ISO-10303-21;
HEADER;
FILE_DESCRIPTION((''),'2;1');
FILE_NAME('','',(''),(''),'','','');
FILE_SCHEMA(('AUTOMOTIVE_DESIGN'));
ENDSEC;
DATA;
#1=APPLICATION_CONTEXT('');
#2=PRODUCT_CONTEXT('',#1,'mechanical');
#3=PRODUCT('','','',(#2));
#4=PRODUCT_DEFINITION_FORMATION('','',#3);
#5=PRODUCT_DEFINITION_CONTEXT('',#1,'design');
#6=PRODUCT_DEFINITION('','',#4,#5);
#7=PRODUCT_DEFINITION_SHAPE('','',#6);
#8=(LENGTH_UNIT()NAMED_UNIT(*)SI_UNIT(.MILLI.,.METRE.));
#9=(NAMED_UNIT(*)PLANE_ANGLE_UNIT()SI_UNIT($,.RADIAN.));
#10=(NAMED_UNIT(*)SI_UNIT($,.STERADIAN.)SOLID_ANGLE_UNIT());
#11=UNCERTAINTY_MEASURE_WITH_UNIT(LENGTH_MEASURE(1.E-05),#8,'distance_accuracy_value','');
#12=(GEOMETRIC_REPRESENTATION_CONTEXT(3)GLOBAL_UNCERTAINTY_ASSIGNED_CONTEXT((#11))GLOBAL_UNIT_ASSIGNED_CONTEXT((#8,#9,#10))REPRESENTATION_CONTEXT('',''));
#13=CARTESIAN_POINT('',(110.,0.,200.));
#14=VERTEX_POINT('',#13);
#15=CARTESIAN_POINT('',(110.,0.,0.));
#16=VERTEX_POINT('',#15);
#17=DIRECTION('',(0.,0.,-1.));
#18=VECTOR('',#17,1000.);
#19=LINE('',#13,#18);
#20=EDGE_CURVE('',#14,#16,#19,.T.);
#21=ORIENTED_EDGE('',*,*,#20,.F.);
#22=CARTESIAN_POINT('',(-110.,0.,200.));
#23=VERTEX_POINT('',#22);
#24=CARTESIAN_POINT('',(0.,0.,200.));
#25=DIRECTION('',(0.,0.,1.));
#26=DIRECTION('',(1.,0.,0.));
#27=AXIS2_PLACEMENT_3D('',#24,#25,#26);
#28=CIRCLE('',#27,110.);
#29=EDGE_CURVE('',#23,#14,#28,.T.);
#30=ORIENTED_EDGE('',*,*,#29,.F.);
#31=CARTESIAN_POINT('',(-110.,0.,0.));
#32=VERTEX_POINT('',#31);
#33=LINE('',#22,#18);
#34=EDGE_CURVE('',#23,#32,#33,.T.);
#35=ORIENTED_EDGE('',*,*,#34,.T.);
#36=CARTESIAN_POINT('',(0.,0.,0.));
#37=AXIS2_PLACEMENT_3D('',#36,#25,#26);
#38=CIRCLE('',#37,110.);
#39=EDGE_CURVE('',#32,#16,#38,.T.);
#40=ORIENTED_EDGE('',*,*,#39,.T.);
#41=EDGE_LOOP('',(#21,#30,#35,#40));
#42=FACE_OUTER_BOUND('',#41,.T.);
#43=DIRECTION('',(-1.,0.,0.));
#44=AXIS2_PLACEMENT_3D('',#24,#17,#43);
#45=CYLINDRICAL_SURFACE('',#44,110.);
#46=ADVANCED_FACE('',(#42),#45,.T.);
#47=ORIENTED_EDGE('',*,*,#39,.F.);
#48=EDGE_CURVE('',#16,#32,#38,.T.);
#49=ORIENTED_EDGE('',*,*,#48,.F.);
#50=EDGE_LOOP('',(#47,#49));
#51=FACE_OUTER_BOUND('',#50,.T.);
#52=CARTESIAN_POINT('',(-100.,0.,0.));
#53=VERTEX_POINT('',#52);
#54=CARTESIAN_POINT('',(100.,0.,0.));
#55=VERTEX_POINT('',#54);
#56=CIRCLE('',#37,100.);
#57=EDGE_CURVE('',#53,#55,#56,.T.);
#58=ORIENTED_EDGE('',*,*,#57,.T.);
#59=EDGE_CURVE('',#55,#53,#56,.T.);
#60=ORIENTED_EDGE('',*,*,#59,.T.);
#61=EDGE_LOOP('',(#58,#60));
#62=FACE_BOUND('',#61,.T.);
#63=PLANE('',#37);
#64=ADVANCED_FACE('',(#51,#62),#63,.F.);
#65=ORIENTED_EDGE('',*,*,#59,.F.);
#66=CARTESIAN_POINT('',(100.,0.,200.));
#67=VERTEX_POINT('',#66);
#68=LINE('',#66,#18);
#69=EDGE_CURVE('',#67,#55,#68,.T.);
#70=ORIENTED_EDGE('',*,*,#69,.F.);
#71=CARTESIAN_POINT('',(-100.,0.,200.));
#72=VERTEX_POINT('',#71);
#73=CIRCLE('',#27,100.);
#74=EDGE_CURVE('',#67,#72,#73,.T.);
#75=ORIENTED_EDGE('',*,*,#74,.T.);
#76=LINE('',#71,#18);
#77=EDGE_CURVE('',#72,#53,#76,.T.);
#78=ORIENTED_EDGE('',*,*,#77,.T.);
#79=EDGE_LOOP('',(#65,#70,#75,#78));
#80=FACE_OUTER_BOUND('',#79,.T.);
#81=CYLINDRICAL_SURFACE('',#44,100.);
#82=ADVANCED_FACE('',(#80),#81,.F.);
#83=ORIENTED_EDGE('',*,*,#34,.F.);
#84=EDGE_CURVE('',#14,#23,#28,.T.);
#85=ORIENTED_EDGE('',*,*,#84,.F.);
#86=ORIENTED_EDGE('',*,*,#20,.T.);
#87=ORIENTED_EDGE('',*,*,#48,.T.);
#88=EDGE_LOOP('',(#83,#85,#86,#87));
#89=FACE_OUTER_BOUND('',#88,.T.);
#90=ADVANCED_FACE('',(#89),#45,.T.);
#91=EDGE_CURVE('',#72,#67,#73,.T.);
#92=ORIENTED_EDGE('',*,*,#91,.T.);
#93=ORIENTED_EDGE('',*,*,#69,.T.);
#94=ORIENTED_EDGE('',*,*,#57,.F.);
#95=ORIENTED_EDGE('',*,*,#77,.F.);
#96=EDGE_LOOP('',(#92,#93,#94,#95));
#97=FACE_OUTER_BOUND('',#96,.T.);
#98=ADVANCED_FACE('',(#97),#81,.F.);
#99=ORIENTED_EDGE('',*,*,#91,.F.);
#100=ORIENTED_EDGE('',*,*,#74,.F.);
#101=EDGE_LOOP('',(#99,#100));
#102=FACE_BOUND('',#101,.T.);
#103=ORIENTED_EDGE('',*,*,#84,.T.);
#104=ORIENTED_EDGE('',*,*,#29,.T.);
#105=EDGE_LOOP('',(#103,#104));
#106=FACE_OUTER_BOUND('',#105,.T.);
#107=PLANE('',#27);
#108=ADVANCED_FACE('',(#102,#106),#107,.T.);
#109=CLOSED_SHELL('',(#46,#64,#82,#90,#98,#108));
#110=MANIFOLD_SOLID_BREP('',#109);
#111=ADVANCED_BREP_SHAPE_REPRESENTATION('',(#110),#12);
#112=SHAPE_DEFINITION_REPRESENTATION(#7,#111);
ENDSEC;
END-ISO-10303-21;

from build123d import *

# Parameters (mm, degrees)
SKETCH_1_R      = 110
SKETCH_1_R_2    = 100
EXTRUDE_1_DEPTH = 200


with BuildPart() as part:
    # 草图1 → 拉伸-薄壁1 (new body)
    with BuildSketch(Plane.XY):
        Circle(SKETCH_1_R)
        Circle(SKETCH_1_R_2, mode=Mode.SUBTRACT)
    extrude(amount=EXTRUDE_1_DEPTH)


solid = part.part
